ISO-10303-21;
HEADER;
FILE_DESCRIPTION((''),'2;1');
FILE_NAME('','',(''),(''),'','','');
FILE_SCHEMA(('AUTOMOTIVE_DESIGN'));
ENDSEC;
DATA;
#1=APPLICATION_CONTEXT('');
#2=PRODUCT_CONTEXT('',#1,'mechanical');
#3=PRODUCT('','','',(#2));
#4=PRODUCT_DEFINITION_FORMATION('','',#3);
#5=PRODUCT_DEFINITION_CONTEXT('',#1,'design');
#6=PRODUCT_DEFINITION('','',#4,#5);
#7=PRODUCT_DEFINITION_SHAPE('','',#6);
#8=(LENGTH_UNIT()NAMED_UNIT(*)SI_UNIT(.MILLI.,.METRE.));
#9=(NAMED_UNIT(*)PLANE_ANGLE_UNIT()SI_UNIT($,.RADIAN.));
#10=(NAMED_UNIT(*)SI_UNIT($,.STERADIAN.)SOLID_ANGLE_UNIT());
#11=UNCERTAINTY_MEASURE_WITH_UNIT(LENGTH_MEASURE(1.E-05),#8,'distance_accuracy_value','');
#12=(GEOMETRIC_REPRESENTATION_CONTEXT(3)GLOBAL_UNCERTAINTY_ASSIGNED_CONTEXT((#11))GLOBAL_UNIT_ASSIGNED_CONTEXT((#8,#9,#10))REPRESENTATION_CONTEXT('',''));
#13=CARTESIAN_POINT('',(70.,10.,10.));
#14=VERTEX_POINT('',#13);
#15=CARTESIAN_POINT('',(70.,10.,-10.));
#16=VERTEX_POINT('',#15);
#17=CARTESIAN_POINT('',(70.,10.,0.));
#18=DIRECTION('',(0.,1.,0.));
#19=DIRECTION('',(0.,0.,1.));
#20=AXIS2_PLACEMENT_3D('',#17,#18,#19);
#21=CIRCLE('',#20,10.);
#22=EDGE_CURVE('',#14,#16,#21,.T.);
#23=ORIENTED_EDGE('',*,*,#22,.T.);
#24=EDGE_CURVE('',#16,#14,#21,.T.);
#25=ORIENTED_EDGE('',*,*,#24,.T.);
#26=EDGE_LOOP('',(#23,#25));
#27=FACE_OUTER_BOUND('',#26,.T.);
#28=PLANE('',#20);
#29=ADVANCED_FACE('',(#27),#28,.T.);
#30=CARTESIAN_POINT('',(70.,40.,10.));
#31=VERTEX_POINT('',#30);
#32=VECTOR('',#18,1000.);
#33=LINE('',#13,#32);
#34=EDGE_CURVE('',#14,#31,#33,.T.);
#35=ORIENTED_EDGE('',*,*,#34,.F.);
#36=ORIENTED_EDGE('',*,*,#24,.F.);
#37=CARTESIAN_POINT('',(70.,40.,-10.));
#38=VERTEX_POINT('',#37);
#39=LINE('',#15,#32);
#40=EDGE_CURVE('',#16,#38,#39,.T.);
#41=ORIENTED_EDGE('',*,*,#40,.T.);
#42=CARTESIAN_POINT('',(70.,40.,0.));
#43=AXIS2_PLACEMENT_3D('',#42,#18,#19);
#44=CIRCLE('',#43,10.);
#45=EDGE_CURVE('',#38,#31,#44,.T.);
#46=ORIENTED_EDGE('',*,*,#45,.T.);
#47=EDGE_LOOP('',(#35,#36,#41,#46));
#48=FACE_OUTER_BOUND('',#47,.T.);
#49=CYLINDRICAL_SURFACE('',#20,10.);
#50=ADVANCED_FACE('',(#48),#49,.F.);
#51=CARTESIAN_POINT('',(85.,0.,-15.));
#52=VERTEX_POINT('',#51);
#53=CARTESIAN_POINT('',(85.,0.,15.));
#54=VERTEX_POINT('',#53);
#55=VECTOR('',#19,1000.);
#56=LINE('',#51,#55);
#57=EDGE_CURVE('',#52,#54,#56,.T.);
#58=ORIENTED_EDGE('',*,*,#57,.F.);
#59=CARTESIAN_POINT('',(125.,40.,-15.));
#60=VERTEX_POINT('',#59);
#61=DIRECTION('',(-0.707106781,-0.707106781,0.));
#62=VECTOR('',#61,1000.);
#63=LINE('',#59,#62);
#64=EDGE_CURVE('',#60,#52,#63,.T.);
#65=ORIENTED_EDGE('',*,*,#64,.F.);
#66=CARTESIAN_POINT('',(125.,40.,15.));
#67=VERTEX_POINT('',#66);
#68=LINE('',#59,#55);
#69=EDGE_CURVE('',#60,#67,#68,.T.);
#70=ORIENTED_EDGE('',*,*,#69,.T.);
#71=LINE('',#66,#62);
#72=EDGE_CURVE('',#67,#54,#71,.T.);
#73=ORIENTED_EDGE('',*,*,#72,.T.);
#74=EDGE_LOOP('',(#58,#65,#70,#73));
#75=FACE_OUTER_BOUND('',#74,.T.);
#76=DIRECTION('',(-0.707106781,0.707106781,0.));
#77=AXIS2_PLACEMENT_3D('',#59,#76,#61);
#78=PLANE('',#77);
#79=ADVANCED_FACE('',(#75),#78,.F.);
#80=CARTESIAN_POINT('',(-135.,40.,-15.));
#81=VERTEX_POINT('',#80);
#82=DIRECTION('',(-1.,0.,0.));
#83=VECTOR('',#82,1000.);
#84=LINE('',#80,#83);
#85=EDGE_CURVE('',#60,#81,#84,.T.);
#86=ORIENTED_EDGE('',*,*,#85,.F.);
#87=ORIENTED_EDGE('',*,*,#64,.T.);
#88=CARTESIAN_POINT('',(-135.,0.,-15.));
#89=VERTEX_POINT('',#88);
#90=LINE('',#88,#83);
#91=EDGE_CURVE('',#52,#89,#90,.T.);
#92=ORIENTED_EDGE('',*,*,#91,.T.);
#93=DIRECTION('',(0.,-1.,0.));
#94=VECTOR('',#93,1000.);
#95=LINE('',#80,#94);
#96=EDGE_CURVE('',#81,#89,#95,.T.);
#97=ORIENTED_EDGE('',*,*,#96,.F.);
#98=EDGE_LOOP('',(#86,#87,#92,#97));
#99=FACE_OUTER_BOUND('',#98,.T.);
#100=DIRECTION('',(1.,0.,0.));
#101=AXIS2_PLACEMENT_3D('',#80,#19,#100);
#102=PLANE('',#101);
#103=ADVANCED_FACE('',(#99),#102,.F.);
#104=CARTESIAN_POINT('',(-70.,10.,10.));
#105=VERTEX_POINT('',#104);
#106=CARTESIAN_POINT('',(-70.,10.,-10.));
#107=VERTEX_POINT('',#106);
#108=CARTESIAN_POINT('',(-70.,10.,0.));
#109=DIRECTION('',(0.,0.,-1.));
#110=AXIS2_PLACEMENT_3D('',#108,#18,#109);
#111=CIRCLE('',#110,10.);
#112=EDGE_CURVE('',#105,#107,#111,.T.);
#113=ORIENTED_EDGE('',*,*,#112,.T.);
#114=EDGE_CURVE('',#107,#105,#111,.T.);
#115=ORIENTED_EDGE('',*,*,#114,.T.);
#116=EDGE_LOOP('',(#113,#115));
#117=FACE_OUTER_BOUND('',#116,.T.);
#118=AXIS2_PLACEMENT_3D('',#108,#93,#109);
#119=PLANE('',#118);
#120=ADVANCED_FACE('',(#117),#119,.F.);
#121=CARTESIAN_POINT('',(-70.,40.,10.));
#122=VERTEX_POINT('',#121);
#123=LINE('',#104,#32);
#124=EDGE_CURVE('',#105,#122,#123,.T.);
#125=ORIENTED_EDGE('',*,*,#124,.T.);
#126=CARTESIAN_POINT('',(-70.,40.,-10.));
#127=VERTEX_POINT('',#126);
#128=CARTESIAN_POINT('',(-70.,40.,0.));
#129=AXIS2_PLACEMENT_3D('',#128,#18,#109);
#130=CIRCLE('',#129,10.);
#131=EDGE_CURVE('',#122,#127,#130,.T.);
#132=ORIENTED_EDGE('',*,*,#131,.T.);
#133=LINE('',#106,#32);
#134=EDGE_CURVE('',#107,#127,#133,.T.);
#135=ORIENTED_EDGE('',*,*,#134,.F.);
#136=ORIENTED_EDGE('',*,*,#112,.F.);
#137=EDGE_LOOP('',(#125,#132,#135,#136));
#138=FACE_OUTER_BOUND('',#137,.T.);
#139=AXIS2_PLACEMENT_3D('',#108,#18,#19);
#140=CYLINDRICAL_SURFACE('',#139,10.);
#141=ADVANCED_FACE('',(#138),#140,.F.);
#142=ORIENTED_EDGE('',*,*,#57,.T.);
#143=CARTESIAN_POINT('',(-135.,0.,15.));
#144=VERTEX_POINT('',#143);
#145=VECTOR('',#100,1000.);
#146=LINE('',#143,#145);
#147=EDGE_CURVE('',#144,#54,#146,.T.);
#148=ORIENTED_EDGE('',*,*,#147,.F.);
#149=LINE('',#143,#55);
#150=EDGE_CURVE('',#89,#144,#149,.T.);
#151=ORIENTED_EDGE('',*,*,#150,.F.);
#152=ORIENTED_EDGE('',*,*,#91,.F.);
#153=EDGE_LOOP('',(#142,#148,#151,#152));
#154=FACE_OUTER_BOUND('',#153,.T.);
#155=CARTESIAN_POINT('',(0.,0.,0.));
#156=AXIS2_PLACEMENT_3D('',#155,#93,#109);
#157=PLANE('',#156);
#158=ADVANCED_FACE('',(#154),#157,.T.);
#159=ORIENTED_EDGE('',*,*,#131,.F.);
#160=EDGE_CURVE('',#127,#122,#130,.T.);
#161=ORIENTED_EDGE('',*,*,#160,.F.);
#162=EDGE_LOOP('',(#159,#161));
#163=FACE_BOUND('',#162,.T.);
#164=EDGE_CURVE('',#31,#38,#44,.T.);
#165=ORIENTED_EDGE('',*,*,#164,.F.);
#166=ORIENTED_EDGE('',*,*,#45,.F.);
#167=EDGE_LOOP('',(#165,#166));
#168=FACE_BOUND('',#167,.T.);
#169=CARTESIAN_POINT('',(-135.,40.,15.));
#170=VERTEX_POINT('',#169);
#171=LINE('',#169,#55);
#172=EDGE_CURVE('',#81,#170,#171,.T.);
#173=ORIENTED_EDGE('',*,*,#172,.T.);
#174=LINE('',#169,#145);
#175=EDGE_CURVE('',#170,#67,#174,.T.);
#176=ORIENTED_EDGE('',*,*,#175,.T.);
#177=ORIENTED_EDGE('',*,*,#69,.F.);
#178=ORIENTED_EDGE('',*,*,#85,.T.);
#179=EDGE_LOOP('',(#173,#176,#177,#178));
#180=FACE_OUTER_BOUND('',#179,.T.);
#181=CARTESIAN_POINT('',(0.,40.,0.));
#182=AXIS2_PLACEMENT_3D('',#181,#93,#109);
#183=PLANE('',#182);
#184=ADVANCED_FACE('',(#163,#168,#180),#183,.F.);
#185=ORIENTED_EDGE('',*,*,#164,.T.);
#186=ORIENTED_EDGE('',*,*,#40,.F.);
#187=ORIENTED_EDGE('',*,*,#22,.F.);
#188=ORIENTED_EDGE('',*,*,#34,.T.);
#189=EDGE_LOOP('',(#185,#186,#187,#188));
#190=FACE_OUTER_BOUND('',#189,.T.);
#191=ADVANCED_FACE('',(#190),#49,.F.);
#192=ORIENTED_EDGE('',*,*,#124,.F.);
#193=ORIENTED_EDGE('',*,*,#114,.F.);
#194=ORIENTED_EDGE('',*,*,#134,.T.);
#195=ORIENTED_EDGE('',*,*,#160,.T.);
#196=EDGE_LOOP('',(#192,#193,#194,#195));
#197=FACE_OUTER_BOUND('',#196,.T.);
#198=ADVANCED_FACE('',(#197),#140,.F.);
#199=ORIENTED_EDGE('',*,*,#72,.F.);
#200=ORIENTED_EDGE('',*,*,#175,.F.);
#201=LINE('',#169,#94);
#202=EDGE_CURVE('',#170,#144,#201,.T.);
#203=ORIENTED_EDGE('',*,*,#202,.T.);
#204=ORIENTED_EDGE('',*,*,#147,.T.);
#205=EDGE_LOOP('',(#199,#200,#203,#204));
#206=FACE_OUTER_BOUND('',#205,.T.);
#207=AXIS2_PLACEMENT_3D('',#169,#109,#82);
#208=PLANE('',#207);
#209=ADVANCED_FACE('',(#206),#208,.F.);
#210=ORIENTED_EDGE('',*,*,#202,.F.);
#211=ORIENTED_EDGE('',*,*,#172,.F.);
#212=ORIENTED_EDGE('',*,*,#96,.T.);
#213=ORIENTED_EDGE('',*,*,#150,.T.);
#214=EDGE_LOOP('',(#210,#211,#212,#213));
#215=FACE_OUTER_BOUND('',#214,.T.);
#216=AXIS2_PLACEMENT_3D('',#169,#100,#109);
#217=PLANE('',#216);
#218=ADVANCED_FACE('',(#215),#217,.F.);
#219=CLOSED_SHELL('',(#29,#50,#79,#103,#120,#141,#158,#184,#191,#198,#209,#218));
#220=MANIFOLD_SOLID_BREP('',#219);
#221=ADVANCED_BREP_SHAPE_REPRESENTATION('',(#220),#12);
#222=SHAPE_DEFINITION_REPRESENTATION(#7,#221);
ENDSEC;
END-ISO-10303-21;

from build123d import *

# Parameters (mm, degrees)
SKETCH_1_W          = 270
SKETCH_1_H          = 30
EXTRUDE_1_DEPTH     = 40
SKETCH_2_R          = 10
CUT_EXTRUDE_2_DEPTH = 30
SKETCH_5_W          = 30
SKETCH_5_H          = 40
CUT_EXTRUDE_4_DEPTH = 10
CUT_EXTRUDE_5_DEPTH = 144.961800489


with BuildPart() as part:
    # 草图1 → 凸台-拉伸1 (new body)
    with BuildSketch(Plane(origin=(0, 0, 0), x_dir=(1, 0, 0), z_dir=(0, 1, 0))):
        Rectangle(SKETCH_1_W, SKETCH_1_H)
    extrude(amount=EXTRUDE_1_DEPTH)

    # 草图2 → 切除-拉伸2 (cut)
    with BuildSketch(Plane(origin=(0, 40, 0), x_dir=(1, 0, 0), z_dir=(0, 1, 0))):
        with Locations(Location((70, 0, 0), (0, 0, 270))):
            Circle(SKETCH_2_R)
        with Locations(Location((-70, 0, 0), (0, 0, 90))):
            Circle(SKETCH_2_R)
    extrude(amount=-CUT_EXTRUDE_2_DEPTH, mode=Mode.SUBTRACT)

    # 草图5 → 切除-拉伸4 (cut)
    with BuildSketch(Plane(origin=(135, 0, 0), x_dir=(0, 0, -1), z_dir=(1, 0, 0))):
        with Locations((0, 20)):
            Rectangle(SKETCH_5_W, SKETCH_5_H)
    extrude(amount=-CUT_EXTRUDE_4_DEPTH, mode=Mode.SUBTRACT)

    # 草图6 → 切除-拉伸5 (cut, through all)
    with BuildSketch(Plane.XY.offset(15)):
        Polygon((125, 40), (85, 0), (125, 0), align=None)
    extrude(amount=-CUT_EXTRUDE_5_DEPTH, mode=Mode.SUBTRACT)


solid = part.part
